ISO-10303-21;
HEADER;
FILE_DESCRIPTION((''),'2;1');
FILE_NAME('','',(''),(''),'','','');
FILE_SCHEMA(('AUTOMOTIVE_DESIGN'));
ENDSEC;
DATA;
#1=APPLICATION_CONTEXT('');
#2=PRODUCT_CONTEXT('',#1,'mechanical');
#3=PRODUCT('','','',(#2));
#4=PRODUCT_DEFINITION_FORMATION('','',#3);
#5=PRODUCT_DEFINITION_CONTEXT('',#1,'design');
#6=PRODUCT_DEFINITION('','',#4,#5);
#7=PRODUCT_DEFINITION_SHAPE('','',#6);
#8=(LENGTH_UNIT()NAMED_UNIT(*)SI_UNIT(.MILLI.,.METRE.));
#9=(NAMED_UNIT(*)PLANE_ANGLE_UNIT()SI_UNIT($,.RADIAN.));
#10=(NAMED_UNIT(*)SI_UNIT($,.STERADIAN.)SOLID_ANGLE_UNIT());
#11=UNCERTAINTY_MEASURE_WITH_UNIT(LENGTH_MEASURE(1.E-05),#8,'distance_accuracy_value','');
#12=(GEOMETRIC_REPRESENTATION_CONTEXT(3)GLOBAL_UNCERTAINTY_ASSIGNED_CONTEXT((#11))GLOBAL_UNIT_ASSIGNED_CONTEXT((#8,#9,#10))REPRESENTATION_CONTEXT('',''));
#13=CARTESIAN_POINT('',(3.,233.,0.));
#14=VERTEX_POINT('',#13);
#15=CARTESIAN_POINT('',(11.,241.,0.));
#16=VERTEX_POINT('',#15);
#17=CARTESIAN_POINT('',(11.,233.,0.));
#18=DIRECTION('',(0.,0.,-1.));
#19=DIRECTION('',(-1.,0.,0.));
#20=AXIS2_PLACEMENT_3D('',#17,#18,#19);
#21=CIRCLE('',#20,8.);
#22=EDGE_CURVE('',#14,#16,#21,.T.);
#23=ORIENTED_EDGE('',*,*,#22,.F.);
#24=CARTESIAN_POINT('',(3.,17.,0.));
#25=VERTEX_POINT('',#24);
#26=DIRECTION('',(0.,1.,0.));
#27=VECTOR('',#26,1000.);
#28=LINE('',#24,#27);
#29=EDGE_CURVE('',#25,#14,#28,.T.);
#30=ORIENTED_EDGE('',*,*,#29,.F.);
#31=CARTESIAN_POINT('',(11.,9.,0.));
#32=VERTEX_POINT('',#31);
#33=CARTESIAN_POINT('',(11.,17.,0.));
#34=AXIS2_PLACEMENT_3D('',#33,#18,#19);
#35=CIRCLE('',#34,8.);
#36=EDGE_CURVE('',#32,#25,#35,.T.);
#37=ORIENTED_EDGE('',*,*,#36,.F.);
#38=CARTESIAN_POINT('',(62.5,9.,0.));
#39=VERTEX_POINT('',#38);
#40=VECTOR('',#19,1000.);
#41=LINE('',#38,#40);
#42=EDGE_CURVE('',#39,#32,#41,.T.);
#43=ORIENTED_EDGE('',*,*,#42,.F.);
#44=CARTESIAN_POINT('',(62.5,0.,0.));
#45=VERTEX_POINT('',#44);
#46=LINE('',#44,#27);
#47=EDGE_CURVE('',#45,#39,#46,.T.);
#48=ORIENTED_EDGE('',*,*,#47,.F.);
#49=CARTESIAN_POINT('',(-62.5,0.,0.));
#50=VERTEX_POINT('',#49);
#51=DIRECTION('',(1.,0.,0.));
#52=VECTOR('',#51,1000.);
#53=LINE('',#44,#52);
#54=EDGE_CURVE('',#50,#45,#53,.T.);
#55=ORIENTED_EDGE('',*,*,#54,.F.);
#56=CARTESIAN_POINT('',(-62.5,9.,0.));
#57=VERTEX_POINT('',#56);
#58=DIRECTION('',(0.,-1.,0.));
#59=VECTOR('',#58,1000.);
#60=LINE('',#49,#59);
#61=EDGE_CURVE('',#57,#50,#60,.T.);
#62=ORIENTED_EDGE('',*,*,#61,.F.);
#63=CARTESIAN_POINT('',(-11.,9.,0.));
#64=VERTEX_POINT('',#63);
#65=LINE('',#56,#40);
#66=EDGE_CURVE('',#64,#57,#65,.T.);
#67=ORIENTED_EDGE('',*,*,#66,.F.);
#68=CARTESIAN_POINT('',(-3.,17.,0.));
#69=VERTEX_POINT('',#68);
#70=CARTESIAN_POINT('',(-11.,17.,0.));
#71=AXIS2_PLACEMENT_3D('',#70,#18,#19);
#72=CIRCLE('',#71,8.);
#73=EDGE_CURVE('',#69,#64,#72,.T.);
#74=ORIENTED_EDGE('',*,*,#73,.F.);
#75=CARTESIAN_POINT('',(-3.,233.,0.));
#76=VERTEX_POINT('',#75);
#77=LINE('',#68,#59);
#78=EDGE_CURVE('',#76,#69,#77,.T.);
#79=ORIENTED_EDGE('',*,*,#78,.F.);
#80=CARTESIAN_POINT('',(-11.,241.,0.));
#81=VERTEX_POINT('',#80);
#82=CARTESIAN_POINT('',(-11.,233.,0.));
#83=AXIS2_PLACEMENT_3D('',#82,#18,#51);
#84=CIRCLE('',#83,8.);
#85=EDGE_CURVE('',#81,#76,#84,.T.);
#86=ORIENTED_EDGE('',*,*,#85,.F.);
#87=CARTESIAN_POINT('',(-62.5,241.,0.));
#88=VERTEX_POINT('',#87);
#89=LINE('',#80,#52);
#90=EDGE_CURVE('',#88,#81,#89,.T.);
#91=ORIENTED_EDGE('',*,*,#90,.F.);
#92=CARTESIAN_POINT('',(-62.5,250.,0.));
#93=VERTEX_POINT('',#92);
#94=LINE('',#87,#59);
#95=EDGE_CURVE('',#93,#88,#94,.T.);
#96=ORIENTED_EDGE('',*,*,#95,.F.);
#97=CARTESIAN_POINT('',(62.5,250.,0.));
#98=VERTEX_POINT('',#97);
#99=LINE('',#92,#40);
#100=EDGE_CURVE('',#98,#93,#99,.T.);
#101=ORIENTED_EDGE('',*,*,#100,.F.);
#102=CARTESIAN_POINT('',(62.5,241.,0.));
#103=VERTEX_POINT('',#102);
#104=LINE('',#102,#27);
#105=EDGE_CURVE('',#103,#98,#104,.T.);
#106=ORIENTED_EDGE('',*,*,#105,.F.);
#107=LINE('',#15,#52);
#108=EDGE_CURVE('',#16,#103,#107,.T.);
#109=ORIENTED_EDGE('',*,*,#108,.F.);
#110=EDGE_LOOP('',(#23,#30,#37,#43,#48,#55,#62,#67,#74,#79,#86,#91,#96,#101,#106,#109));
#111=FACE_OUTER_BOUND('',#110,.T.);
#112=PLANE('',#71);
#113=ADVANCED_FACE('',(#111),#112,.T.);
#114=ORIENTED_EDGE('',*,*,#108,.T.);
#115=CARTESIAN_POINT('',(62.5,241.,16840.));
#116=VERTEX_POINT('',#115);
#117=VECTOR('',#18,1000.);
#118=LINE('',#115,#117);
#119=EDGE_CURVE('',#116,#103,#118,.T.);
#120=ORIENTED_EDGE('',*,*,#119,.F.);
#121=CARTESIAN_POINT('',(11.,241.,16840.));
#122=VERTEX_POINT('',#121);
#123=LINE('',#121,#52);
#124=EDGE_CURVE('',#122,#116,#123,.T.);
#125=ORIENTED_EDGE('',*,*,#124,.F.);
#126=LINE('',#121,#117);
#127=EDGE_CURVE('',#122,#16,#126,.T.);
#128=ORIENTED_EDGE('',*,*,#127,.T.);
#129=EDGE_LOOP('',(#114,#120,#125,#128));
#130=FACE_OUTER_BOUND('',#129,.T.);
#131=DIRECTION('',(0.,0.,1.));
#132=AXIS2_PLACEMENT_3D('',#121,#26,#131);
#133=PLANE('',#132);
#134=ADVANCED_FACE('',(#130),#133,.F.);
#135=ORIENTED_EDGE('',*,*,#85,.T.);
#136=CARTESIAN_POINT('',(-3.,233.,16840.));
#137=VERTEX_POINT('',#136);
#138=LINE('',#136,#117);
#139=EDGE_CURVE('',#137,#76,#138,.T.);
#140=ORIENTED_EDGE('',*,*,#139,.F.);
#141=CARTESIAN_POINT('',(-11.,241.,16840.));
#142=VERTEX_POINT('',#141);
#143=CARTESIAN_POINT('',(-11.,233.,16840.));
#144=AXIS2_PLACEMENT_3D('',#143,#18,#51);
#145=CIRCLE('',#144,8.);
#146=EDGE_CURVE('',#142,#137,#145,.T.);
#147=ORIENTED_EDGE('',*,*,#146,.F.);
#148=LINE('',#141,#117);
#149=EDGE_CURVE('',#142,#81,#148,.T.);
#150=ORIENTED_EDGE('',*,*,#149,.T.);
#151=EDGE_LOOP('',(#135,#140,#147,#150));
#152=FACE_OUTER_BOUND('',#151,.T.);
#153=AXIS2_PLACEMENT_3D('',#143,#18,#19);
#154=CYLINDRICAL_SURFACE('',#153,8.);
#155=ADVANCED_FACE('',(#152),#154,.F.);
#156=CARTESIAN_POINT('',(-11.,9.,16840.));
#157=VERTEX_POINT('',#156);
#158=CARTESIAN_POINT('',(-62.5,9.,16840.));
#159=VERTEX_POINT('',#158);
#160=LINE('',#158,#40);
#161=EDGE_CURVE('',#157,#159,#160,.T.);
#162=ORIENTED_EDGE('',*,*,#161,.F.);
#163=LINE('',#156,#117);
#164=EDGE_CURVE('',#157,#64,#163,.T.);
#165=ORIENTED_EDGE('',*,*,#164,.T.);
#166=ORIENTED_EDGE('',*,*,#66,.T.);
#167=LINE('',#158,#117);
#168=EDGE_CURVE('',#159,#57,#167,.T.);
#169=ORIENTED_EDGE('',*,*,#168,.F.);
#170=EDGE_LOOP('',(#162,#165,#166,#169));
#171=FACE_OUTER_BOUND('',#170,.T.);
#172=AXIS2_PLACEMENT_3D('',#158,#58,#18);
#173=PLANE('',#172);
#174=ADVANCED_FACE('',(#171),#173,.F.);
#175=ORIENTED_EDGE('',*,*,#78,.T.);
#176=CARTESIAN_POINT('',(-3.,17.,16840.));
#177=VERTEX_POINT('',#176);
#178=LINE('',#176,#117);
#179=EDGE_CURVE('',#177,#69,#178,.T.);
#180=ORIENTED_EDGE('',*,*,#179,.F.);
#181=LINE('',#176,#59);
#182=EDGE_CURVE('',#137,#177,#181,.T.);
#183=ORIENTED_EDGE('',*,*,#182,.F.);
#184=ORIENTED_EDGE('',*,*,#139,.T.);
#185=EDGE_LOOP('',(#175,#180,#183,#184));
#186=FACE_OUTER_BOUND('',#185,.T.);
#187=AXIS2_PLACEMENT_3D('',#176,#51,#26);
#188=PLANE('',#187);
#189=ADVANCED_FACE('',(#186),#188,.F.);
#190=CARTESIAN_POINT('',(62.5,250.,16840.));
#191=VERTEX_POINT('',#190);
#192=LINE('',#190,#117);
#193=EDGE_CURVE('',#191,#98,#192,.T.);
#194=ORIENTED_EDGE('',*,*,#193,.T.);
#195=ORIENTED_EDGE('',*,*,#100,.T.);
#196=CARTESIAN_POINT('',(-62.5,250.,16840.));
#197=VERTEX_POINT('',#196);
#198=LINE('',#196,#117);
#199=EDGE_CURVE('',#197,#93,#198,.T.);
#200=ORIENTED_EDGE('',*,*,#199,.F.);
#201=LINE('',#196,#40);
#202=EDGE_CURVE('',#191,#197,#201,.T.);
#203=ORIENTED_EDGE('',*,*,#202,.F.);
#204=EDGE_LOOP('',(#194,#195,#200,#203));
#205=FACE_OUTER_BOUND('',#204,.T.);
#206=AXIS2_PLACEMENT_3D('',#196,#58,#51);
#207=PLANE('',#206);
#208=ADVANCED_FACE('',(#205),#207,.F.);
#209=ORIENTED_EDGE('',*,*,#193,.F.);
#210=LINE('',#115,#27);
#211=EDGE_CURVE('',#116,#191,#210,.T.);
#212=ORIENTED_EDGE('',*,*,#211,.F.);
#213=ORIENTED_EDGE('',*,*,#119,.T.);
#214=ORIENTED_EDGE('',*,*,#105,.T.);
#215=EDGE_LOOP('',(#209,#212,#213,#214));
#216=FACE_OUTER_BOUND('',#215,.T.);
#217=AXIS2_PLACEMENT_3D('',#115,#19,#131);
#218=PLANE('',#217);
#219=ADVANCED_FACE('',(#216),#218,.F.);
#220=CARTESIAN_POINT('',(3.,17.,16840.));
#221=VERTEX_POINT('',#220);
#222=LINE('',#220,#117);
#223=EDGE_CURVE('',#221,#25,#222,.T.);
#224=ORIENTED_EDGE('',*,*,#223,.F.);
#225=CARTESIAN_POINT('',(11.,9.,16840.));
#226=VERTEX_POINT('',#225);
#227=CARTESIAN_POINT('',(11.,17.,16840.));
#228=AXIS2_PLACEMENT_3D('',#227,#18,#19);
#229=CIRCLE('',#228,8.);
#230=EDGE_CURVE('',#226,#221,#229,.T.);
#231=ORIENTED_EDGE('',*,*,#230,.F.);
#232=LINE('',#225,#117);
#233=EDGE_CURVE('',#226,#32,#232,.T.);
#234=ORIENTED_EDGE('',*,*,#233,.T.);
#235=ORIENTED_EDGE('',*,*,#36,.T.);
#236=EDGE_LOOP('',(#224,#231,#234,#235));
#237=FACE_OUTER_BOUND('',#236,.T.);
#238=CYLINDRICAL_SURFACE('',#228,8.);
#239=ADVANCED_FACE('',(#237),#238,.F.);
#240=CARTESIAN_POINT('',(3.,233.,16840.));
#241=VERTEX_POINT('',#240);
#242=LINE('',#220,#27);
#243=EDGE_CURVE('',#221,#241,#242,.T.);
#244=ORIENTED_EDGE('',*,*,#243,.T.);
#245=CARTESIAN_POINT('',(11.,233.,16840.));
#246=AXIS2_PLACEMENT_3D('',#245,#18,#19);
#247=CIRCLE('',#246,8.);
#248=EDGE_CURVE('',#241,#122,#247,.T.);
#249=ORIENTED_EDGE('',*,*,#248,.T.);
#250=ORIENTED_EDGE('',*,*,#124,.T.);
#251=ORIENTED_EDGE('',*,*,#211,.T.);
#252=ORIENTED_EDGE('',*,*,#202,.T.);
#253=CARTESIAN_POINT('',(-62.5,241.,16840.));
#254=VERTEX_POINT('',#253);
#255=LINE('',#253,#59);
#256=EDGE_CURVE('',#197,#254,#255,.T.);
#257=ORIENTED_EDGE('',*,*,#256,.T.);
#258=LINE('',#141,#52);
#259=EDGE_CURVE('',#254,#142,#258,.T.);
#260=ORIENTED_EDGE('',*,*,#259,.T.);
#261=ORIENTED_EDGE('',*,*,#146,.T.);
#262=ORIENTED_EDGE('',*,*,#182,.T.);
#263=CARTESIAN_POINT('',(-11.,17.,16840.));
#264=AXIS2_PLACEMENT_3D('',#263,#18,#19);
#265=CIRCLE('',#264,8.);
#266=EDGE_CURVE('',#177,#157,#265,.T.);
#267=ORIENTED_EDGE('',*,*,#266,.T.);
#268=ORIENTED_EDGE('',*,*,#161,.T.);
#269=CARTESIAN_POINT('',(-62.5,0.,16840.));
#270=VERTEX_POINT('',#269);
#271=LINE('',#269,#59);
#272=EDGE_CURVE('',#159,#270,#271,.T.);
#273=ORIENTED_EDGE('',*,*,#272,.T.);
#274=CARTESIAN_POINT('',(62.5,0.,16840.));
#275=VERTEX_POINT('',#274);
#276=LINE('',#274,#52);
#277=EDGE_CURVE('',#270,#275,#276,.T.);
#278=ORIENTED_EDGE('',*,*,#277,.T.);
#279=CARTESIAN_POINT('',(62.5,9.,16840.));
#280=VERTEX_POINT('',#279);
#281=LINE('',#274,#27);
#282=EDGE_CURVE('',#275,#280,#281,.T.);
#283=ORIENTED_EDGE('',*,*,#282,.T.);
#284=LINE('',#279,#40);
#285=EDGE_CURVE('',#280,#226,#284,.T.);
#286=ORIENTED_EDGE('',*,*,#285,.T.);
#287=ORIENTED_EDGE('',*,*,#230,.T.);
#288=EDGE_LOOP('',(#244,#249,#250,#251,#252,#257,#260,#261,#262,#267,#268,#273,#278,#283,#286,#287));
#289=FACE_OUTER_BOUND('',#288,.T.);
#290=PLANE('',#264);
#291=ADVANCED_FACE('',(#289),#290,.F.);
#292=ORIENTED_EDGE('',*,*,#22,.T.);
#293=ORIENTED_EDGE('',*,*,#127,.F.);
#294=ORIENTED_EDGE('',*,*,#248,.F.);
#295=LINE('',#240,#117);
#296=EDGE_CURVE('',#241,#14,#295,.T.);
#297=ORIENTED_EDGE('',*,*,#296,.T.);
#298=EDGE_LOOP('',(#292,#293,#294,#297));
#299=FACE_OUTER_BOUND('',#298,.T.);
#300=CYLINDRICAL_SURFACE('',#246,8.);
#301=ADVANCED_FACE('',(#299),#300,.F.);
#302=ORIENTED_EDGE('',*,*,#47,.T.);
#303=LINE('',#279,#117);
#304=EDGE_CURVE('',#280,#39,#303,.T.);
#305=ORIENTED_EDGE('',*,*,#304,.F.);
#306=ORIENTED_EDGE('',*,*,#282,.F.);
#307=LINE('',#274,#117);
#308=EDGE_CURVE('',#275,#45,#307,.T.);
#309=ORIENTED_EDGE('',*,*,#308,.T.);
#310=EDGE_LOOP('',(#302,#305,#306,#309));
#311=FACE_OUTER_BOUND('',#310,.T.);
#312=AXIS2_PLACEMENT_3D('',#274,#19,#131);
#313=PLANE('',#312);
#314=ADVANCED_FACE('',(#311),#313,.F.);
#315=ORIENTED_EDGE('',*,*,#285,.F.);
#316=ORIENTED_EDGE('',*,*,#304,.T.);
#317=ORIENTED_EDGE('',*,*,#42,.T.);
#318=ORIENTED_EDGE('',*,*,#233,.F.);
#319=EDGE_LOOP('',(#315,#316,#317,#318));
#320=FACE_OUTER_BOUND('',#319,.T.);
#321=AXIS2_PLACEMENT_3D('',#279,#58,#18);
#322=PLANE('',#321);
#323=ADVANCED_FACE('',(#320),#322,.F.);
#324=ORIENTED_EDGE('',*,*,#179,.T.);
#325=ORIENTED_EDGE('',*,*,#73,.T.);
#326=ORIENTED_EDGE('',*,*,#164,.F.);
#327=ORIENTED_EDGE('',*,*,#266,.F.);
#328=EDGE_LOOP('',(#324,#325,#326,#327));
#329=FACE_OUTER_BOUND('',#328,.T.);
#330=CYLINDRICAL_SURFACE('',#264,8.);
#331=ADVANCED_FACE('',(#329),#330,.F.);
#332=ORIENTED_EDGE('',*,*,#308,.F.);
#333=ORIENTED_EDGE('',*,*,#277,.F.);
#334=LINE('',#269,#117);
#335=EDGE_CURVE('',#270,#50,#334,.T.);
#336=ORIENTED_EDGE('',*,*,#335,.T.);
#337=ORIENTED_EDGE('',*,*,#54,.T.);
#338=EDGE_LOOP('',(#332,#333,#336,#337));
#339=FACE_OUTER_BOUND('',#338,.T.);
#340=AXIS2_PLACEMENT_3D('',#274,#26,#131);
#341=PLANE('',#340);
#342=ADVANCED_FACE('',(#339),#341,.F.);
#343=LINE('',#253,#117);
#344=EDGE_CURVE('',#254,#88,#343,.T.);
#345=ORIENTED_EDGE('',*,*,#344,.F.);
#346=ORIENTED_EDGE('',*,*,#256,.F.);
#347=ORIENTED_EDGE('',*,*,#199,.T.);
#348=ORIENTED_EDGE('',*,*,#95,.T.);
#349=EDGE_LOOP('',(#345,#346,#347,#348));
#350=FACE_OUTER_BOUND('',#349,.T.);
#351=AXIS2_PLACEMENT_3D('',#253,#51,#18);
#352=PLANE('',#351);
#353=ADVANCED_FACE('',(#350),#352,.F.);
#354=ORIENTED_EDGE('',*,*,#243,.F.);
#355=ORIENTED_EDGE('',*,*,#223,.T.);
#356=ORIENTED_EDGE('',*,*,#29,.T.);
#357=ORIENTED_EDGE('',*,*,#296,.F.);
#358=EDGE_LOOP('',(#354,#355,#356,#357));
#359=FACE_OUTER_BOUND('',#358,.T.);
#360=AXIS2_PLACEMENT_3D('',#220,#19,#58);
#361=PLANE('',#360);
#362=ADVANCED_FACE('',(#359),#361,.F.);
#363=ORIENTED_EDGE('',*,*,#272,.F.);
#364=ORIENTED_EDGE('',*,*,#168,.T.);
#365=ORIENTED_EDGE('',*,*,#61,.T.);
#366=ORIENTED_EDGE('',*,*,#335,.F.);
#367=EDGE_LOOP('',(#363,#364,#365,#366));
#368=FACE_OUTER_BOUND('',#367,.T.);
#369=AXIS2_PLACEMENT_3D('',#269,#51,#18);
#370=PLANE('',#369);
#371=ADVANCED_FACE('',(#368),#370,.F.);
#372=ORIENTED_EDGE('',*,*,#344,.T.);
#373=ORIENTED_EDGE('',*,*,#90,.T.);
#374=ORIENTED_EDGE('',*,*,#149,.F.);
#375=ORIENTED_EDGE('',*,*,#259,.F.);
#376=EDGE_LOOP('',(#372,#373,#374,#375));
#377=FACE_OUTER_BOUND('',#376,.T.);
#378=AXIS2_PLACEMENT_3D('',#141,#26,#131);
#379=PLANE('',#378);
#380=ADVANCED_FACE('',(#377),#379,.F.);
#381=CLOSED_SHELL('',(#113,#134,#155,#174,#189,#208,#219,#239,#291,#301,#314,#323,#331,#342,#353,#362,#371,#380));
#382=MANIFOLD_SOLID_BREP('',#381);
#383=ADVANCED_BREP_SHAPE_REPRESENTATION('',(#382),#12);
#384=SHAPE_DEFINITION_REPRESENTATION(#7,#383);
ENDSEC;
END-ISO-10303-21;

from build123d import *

# Parameters (mm, degrees)
BOSS_EXTRUDE1_DEPTH = 16840


with BuildPart() as part:
    # Sketch1 → Boss-Extrude1 (new body)
    with BuildSketch(Plane.XY):
        with BuildLine():
            Line((62.5, 0), (-62.5, 0))
            Line((-62.5, 0), (-62.5, 9))
            Line((-62.5, 9), (-11, 9))
            ThreePointArc((-11, 9), (-5.343145751, 11.343145751), (-3, 17))
            Line((-3, 17), (-3, 233))
            ThreePointArc((-3, 233), (-5.343145751, 238.656854249), (-11, 241))
            Line((-11, 241), (-62.5, 241))
            Line((-62.5, 241), (-62.5, 250))
            Line((-62.5, 250), (62.5, 250))
            Line((62.5, 250), (62.5, 241))
            Line((62.5, 241), (11, 241))
            ThreePointArc((11, 241), (5.343145751, 238.656854249), (3, 233))
            Line((3, 233), (3, 17))
            ThreePointArc((3, 17), (5.343145751, 11.343145751), (11, 9))
            Line((11, 9), (62.5, 9))
            Line((62.5, 9), (62.5, 0))
        make_face()
    extrude(amount=BOSS_EXTRUDE1_DEPTH)


solid = part.part
